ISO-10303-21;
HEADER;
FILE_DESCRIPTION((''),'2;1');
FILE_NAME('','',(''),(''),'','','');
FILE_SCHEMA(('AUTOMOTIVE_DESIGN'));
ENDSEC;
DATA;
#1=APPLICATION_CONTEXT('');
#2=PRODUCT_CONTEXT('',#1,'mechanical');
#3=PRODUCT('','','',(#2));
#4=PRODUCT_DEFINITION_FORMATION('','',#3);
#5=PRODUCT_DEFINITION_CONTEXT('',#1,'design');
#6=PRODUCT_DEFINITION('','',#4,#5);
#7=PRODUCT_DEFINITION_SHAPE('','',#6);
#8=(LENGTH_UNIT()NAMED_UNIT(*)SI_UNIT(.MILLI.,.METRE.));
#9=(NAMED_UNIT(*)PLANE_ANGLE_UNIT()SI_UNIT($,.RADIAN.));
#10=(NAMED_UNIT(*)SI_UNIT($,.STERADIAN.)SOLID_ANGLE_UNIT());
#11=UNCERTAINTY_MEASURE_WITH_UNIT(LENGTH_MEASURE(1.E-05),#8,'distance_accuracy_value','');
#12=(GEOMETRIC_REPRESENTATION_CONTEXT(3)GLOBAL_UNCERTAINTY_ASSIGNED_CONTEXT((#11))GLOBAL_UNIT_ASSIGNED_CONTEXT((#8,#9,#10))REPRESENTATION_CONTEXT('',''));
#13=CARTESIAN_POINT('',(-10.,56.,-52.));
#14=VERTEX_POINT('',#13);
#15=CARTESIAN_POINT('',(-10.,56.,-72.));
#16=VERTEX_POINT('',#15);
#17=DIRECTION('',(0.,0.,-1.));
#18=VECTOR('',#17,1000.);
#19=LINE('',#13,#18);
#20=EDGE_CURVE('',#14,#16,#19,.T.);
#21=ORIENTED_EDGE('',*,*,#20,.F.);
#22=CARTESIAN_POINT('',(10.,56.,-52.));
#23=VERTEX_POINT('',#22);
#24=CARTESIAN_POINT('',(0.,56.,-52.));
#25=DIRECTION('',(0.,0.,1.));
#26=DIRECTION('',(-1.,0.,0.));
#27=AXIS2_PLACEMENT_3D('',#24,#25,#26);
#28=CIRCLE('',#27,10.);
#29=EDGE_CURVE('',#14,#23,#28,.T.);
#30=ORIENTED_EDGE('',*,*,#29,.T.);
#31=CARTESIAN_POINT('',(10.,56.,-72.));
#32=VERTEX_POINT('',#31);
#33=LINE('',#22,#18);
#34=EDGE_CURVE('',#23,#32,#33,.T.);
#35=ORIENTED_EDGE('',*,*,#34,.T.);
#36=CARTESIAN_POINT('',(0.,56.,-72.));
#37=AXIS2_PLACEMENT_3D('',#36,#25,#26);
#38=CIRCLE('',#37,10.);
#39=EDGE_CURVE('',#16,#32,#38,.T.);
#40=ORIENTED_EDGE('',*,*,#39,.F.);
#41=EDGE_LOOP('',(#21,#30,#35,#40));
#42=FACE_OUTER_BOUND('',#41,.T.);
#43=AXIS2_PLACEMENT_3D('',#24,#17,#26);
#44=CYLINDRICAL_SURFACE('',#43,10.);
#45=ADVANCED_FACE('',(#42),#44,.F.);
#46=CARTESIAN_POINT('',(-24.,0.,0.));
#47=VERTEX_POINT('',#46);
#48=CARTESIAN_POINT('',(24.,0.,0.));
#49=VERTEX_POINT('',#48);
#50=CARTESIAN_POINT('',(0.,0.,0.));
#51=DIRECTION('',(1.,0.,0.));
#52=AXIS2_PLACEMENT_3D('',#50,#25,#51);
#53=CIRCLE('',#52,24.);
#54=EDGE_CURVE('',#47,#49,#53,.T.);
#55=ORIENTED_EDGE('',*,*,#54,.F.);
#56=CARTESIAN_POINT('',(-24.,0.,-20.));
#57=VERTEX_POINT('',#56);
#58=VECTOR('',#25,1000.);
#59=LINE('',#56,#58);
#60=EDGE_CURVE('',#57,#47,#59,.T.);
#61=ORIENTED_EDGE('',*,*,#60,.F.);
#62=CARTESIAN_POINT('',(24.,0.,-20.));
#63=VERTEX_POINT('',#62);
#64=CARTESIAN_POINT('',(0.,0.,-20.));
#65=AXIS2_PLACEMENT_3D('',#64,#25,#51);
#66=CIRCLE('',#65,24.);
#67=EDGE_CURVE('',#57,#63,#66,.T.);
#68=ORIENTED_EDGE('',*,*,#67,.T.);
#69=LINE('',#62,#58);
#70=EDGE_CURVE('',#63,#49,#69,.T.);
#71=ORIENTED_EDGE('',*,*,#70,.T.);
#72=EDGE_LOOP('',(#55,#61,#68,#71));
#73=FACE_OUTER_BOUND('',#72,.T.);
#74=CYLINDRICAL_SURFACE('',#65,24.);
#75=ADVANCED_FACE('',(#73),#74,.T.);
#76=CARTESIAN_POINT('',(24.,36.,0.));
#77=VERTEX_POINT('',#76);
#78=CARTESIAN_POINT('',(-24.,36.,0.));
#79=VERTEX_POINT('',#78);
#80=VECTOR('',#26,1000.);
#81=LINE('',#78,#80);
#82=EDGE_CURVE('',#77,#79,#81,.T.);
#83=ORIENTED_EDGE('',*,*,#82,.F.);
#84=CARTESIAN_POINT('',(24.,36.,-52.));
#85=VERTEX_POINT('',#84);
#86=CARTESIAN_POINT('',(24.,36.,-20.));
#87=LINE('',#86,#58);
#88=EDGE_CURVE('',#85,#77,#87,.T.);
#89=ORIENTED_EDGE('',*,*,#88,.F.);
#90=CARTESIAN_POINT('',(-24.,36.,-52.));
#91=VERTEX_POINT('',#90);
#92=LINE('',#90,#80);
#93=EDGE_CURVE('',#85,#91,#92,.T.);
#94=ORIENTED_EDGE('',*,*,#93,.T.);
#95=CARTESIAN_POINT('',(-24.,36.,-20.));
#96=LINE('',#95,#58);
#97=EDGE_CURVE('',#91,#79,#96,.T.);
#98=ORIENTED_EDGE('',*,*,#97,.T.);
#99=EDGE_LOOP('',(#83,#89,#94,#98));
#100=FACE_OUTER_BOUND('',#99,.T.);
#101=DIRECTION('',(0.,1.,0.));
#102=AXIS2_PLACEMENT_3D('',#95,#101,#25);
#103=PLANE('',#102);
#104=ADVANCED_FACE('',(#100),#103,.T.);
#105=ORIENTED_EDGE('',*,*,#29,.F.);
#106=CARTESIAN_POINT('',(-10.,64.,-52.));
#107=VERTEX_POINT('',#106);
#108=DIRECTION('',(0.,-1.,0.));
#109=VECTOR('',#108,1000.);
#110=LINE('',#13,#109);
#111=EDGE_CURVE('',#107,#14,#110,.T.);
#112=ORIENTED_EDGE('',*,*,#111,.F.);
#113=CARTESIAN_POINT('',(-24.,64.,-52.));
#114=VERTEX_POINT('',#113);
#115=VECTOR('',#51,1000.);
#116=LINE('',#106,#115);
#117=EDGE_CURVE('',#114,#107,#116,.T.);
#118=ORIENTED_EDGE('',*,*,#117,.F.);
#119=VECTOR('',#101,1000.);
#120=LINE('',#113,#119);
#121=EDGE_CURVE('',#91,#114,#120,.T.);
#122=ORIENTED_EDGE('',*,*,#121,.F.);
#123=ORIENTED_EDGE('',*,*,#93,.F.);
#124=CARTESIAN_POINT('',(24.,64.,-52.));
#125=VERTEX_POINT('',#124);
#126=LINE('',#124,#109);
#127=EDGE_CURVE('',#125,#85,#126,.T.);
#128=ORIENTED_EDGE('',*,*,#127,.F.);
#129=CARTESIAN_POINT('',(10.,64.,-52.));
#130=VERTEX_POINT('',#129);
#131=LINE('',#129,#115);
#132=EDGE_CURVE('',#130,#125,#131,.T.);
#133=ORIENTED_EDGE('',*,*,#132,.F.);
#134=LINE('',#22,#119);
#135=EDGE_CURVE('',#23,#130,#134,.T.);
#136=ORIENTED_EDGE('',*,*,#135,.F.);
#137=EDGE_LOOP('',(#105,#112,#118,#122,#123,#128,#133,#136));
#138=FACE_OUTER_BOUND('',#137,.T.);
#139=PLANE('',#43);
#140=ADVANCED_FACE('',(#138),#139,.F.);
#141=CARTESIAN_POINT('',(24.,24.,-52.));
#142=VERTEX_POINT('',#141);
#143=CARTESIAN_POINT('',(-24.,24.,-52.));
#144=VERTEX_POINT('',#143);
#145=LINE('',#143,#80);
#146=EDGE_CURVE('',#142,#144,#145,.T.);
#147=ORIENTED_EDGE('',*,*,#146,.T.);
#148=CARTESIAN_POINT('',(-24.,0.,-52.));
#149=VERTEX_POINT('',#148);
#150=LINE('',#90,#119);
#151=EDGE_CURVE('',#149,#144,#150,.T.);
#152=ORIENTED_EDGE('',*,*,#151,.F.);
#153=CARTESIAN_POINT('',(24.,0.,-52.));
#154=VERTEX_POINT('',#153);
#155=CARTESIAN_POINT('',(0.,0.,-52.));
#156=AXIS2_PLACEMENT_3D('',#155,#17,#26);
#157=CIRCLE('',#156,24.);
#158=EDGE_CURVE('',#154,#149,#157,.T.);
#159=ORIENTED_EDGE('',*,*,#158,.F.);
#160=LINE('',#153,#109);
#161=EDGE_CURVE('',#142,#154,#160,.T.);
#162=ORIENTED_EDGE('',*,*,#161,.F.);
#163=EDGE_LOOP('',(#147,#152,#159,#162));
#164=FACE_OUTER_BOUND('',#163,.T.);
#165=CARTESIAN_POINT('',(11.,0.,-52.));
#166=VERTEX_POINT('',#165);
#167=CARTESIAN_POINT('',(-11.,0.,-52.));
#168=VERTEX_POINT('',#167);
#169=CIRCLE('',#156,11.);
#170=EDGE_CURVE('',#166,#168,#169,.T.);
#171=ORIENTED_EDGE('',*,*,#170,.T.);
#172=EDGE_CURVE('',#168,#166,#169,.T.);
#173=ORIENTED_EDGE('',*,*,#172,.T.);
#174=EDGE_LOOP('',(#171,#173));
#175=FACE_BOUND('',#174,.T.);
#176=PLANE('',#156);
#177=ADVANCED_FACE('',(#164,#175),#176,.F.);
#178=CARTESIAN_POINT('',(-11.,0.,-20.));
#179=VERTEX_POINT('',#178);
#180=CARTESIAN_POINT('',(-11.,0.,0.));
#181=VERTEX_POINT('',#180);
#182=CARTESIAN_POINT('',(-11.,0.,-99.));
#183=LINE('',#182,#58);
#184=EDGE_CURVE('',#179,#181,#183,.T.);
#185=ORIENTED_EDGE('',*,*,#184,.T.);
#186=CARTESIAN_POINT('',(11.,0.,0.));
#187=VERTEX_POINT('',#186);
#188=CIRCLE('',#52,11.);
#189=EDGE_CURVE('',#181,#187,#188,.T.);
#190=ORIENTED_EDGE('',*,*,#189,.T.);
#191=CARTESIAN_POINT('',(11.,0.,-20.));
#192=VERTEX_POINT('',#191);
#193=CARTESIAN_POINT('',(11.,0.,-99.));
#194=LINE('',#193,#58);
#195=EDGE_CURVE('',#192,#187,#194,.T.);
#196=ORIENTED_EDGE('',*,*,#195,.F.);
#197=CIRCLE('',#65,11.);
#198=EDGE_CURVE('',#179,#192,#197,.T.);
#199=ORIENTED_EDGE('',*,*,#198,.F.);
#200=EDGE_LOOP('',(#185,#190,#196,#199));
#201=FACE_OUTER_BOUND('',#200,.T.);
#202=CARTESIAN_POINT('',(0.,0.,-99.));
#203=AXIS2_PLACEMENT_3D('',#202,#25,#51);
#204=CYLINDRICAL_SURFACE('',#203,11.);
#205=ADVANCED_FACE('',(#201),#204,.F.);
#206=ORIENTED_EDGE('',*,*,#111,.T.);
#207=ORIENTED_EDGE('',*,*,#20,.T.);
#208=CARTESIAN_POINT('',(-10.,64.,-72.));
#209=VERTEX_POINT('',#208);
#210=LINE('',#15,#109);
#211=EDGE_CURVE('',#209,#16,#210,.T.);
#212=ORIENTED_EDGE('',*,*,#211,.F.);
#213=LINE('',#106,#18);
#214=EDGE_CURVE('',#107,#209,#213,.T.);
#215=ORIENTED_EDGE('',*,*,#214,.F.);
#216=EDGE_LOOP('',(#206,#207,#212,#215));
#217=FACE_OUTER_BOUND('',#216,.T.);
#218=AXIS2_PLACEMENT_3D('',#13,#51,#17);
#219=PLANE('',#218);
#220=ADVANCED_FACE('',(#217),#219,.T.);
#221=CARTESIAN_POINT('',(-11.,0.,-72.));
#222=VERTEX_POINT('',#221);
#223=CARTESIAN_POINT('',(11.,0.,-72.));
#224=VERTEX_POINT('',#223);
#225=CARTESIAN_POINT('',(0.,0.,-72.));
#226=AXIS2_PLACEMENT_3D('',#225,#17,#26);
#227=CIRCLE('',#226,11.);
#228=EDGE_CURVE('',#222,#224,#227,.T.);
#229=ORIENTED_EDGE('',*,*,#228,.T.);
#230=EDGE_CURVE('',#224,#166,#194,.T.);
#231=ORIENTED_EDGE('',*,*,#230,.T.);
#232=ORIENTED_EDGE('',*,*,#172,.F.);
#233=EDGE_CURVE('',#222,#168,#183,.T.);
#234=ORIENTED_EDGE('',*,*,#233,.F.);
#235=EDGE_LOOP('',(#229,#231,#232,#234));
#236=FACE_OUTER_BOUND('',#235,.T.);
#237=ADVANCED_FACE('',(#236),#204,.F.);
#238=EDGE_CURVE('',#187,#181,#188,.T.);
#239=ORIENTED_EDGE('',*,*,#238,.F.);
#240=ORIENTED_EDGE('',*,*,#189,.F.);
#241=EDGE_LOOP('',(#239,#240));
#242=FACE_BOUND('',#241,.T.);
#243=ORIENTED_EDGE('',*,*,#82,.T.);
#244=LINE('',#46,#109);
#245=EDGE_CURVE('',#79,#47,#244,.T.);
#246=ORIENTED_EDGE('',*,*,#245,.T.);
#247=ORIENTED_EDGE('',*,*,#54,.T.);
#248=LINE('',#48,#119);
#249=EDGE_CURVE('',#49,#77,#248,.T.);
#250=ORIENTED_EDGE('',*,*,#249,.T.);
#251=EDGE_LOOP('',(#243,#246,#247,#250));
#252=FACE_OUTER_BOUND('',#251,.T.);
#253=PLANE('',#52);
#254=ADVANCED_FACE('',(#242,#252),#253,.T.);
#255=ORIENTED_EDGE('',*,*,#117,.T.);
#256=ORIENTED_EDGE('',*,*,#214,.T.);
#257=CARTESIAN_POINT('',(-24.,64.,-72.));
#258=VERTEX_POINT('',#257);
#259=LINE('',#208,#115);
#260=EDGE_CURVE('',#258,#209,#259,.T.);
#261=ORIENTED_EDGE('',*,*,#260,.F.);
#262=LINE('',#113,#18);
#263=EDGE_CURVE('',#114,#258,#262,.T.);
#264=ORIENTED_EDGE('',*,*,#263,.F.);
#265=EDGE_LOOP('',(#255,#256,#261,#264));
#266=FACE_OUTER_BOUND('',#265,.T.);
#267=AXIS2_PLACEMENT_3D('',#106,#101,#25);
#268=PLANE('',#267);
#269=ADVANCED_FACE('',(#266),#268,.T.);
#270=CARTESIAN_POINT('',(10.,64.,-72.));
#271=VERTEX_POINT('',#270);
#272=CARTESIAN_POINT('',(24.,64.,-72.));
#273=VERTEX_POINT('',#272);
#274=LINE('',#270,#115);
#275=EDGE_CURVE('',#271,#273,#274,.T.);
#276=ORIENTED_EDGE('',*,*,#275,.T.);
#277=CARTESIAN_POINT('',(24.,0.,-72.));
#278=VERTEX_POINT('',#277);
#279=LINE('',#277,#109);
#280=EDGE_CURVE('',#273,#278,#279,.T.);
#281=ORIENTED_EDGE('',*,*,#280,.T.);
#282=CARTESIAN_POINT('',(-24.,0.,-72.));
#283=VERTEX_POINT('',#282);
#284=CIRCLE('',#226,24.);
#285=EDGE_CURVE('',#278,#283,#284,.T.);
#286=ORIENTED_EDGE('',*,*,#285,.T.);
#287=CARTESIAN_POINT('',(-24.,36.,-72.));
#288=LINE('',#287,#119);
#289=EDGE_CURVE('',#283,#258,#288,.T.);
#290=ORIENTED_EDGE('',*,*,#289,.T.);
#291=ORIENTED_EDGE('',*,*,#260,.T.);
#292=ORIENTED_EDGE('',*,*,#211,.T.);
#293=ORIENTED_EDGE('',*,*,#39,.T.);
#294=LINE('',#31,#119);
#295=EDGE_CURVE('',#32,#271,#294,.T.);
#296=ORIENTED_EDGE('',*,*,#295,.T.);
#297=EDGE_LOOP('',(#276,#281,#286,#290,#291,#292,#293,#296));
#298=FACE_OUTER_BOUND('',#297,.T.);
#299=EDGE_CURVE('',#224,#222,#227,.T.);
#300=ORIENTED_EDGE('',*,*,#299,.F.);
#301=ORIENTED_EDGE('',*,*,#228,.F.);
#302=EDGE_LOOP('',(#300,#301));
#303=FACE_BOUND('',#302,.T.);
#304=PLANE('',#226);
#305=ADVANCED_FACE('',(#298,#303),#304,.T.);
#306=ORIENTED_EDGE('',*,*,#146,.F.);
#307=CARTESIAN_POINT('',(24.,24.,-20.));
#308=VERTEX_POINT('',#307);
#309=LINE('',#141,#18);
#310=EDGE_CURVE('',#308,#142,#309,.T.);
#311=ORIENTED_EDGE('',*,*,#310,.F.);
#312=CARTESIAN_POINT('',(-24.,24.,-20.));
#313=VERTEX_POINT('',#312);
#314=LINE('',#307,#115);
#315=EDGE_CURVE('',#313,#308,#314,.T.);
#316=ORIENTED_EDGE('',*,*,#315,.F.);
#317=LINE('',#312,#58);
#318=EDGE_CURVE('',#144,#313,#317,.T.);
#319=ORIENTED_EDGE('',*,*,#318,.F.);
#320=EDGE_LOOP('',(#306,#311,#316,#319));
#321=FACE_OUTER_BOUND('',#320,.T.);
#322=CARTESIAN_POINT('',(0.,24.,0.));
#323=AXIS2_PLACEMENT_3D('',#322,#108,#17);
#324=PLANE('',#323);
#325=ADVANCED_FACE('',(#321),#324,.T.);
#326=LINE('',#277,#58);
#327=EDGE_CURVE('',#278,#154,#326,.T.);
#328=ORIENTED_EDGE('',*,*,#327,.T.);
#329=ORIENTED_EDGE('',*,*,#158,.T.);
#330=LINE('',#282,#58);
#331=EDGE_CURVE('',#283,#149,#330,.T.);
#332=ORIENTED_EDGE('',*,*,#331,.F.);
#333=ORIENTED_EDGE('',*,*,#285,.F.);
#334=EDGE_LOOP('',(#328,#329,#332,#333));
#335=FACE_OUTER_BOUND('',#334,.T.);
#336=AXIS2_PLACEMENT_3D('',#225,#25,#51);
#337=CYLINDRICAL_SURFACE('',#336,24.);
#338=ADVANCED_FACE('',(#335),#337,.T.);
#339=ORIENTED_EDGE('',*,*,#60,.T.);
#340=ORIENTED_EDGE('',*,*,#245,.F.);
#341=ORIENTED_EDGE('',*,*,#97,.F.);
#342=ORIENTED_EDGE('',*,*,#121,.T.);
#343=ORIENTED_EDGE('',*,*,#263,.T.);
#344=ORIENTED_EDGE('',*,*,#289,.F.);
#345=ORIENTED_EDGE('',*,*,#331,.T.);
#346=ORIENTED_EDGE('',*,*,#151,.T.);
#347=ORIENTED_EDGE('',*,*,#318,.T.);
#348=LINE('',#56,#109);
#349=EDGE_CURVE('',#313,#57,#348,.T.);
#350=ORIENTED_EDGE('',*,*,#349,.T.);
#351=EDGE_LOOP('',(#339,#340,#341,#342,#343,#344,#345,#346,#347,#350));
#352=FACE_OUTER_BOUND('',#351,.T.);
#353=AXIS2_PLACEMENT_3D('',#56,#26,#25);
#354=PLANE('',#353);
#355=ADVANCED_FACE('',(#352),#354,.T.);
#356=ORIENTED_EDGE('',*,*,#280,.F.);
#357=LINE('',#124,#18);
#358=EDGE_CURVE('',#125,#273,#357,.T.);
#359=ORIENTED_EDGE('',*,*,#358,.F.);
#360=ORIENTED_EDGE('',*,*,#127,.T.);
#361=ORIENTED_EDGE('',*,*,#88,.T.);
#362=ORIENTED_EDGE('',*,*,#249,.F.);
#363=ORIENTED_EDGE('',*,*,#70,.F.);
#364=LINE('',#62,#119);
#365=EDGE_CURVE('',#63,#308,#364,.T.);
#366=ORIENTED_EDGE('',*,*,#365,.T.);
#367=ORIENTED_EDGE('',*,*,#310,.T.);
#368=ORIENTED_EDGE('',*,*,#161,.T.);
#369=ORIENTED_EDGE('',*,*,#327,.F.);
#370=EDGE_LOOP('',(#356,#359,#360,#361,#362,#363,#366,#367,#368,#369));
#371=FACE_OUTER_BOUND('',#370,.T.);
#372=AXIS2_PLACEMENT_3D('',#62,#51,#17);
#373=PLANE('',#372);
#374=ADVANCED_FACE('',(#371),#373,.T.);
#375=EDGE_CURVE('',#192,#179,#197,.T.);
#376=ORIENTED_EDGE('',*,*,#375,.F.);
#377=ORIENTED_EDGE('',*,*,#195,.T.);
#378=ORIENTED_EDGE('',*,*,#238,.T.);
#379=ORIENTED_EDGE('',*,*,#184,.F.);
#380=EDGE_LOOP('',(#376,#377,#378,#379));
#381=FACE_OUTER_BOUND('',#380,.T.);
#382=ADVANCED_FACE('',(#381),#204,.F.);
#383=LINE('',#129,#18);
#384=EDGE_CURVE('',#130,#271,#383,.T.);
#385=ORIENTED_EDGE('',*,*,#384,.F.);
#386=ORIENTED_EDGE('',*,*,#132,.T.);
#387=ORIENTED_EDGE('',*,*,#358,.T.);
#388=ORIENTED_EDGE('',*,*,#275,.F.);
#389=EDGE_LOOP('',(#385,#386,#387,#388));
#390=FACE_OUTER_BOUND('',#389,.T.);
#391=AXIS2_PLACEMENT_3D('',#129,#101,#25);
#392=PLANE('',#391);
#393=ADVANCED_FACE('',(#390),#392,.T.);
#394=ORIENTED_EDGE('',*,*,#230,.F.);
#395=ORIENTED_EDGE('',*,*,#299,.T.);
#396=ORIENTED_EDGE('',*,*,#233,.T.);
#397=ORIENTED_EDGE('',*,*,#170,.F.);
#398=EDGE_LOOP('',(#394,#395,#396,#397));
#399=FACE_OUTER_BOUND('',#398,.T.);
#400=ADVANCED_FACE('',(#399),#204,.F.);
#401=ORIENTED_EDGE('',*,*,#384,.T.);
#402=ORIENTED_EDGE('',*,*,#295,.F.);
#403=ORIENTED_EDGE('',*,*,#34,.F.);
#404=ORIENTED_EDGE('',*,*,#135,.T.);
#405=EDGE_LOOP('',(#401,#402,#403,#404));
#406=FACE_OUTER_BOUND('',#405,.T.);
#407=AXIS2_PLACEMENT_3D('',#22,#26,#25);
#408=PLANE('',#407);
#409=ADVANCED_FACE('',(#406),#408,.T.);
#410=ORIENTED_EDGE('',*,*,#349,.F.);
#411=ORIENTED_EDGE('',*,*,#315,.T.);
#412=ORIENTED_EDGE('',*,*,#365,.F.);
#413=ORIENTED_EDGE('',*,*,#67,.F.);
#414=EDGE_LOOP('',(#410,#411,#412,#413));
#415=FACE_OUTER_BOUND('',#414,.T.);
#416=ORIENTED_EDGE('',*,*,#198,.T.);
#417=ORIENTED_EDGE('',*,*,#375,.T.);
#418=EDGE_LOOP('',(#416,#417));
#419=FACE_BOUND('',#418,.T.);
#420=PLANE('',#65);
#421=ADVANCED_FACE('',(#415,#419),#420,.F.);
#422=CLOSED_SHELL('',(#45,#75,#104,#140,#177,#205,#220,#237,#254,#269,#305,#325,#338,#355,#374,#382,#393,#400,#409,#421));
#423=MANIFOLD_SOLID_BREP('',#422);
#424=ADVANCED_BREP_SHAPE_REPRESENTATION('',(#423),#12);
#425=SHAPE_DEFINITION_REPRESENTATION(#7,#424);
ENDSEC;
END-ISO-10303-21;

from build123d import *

# Parameters (mm, degrees)
FRONT_LUG_DEPTH            = 20
REAR_LUG_DEPTH             = 20
CONNECTING_BLOCK_PROFILE_W = 48
CONNECTING_BLOCK_PROFILE_H = 32
CONNECTING_BLOCK_DEPTH     = 12
CLEVIS_FORK_DEPTH          = 20
PIN_HOLE_PROFILE_R         = 11
PIN_HOLE_DEPTH             = 99


with BuildPart() as part:
    # Front Lug Profile → Front Lug (new body)
    with BuildSketch(Plane.XY):
        with BuildLine():
            Line((24, 0), (24, 36))
            Line((24, 36), (-24, 36))
            Line((-24, 36), (-24, 0))
            ThreePointArc((-24, 0), (0, -24), (24, 0))
        make_face()
    extrude(amount=-FRONT_LUG_DEPTH)



with BuildPart() as body_2:
    # Rear Lug Profile → Rear Lug (new body)
    with BuildSketch(Plane(origin=(0, 0, -52), x_dir=(-1, 0, 0), z_dir=(0, 0, -1))):
        with BuildLine():
            Line((-24, 0), (-24, 36))
            Line((-24, 36), (24, 36))
            Line((24, 36), (24, 0))
            ThreePointArc((24, 0), (0, -24), (-24, 0))
        make_face()
    extrude(amount=REAR_LUG_DEPTH)


with BuildPart() as part_1:
    add(part.part)

    add(body_2.part)  # Connecting Block merges body 2
    # Connecting Block Profile → Connecting Block (add)
    with BuildSketch(Plane(origin=(0, 36, 0), x_dir=(1, 0, 0), z_dir=(0, 1, 0))):
        with Locations((0, 36)):
            Rectangle(CONNECTING_BLOCK_PROFILE_W, CONNECTING_BLOCK_PROFILE_H)
    extrude(amount=-CONNECTING_BLOCK_DEPTH)

    # Clevis Fork Profile → Clevis Fork (add)
    with BuildSketch(Plane(origin=(0, 0, -72), x_dir=(-1, 0, 0), z_dir=(0, 0, -1))):
        with BuildLine():
            Line((10, 56), (10, 64))
            Line((10, 64), (24, 64))
            Line((24, 64), (24, 36))
            Line((24, 36), (-24, 36))
            Line((-24, 36), (-24, 64))
            Line((-24, 64), (-10, 64))
            Line((-10, 64), (-10, 56))
            ThreePointArc((-10, 56), (0, 46), (10, 56))
        make_face()
    extrude(amount=-CLEVIS_FORK_DEPTH)

    # Pin Hole Profile → Pin Hole (cut)
    with BuildSketch(Plane.XY):
        with Locations(Location((0, 0, 0), (0, 0, 180))):
            Circle(PIN_HOLE_PROFILE_R)
    extrude(amount=-PIN_HOLE_DEPTH, mode=Mode.SUBTRACT)


solid = part_1.part
